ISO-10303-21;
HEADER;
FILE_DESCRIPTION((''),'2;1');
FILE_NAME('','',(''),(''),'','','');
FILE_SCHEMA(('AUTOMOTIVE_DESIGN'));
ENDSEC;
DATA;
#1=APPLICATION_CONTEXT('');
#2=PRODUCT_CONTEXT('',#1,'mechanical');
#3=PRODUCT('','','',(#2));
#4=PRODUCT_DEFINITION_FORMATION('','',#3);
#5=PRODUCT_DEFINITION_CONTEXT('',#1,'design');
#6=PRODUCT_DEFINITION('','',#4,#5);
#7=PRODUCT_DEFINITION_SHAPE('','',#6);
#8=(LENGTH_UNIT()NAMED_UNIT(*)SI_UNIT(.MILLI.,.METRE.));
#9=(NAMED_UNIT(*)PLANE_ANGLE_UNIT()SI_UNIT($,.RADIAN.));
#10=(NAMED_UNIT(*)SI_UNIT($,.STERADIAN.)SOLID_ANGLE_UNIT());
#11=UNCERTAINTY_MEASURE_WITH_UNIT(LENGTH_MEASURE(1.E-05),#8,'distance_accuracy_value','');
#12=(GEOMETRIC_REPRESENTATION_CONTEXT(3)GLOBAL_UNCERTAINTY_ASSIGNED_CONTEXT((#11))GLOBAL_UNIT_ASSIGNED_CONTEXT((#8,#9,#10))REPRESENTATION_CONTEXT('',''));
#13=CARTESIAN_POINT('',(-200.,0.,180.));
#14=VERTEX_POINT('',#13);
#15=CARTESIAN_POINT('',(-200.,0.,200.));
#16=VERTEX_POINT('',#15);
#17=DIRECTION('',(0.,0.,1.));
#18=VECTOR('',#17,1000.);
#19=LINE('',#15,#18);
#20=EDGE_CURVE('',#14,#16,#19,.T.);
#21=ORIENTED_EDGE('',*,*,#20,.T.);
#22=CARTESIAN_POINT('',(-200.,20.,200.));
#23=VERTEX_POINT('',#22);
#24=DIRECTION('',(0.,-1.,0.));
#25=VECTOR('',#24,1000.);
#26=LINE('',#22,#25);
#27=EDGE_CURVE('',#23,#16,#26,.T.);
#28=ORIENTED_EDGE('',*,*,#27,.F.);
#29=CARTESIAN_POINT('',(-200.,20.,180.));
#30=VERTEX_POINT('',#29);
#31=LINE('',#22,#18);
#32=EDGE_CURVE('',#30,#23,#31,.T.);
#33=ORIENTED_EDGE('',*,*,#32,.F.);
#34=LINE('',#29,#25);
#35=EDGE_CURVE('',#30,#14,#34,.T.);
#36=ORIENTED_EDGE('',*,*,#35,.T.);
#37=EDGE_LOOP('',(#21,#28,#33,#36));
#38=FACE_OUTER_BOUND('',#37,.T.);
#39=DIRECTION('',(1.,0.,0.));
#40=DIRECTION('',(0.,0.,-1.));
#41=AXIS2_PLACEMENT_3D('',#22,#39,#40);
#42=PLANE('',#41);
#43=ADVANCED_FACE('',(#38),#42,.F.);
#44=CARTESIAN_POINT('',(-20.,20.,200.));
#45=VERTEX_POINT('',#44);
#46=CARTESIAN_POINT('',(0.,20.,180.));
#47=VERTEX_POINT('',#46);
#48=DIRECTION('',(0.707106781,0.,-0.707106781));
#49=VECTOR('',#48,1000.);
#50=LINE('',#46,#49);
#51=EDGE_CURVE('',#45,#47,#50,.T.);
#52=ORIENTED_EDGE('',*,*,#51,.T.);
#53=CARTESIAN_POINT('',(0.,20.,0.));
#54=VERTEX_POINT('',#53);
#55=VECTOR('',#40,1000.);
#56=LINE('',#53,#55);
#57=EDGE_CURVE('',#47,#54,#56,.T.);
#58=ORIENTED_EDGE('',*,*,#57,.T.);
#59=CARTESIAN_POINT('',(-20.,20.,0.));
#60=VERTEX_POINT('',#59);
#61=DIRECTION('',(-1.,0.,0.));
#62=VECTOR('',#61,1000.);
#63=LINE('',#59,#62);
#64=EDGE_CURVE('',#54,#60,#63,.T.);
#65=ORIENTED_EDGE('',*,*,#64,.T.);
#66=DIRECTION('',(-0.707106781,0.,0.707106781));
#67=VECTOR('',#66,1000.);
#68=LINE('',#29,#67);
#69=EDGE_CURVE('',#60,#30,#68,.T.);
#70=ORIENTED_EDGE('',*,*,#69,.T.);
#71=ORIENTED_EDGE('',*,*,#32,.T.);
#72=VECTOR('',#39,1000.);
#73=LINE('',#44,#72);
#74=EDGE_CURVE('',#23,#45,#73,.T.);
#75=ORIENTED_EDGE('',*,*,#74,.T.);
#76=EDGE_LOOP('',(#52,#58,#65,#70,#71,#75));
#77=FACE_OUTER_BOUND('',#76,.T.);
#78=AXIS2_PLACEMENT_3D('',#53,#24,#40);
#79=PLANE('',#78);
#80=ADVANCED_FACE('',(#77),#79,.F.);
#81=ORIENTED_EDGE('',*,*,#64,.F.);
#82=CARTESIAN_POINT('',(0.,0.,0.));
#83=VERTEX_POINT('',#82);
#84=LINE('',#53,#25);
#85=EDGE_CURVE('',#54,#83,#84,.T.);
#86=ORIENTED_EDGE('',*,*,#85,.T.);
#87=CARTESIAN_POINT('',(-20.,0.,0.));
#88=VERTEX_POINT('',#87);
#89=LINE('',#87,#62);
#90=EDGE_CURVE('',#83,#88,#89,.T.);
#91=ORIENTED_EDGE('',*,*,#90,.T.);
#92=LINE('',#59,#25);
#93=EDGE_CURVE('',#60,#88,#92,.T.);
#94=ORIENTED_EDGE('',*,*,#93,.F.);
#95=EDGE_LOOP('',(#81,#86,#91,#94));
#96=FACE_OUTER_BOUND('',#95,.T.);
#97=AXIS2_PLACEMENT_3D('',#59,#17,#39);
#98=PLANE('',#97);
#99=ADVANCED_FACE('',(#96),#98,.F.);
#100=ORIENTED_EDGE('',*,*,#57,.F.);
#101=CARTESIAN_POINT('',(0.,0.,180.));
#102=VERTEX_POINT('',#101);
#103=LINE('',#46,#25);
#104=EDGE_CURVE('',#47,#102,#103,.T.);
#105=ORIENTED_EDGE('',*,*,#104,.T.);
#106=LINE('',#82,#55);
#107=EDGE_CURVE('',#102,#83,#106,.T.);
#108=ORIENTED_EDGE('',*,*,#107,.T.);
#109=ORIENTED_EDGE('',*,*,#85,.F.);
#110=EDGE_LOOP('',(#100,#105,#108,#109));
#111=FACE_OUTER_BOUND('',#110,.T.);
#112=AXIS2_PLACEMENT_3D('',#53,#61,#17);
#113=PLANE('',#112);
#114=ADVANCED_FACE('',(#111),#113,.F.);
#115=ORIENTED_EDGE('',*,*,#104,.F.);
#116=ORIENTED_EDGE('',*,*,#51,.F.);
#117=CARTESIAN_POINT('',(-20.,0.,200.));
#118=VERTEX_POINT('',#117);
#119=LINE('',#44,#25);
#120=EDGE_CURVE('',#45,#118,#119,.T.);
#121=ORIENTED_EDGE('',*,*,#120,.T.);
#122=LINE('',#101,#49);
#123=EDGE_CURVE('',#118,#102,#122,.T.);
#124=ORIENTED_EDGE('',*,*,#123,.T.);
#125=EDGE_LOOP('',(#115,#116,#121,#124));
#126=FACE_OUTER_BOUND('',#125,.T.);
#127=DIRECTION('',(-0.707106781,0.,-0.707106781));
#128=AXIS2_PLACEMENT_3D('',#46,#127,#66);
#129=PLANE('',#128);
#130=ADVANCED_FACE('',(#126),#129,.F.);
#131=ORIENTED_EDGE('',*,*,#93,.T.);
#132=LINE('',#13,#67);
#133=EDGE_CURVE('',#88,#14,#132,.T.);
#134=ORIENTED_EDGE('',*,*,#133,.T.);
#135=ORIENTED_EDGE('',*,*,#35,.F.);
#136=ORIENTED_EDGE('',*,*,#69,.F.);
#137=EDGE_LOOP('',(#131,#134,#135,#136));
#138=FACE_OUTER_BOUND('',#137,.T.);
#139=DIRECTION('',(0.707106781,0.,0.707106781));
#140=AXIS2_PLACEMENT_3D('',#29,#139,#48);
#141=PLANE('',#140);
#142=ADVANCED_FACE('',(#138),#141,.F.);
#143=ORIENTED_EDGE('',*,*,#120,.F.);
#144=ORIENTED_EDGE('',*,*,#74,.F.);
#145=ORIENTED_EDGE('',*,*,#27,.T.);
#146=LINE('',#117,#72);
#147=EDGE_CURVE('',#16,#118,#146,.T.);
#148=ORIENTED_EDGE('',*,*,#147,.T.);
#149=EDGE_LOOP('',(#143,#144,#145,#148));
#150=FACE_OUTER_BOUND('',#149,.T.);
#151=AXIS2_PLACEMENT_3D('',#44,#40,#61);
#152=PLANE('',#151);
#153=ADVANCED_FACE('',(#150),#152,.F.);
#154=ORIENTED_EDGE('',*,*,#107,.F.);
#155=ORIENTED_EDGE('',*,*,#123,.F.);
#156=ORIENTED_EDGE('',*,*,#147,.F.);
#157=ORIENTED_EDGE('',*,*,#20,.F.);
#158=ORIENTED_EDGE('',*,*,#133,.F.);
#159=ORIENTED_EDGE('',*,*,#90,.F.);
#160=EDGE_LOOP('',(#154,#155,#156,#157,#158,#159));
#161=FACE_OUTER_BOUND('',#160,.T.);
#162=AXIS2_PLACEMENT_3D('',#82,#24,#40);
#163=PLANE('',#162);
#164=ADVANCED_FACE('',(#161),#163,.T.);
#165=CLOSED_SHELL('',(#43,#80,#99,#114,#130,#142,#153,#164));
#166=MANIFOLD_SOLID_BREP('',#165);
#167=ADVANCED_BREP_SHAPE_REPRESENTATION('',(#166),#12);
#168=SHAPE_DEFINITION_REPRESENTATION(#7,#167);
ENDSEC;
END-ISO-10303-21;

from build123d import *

# Parameters (mm, degrees)
EXTRUDE_1_DEPTH = 20


with BuildPart() as part:
    # 草图1 → 凸台-拉伸1 (new body)
    with BuildSketch(Plane(origin=(0, 0, 0), x_dir=(1, 0, 0), z_dir=(0, 1, 0))):
        Polygon((0, 0), (0, -180), (-20, -200), (-200, -200), (-200, -180), (-20, 0), align=None)
    extrude(amount=EXTRUDE_1_DEPTH)


solid = part.part
